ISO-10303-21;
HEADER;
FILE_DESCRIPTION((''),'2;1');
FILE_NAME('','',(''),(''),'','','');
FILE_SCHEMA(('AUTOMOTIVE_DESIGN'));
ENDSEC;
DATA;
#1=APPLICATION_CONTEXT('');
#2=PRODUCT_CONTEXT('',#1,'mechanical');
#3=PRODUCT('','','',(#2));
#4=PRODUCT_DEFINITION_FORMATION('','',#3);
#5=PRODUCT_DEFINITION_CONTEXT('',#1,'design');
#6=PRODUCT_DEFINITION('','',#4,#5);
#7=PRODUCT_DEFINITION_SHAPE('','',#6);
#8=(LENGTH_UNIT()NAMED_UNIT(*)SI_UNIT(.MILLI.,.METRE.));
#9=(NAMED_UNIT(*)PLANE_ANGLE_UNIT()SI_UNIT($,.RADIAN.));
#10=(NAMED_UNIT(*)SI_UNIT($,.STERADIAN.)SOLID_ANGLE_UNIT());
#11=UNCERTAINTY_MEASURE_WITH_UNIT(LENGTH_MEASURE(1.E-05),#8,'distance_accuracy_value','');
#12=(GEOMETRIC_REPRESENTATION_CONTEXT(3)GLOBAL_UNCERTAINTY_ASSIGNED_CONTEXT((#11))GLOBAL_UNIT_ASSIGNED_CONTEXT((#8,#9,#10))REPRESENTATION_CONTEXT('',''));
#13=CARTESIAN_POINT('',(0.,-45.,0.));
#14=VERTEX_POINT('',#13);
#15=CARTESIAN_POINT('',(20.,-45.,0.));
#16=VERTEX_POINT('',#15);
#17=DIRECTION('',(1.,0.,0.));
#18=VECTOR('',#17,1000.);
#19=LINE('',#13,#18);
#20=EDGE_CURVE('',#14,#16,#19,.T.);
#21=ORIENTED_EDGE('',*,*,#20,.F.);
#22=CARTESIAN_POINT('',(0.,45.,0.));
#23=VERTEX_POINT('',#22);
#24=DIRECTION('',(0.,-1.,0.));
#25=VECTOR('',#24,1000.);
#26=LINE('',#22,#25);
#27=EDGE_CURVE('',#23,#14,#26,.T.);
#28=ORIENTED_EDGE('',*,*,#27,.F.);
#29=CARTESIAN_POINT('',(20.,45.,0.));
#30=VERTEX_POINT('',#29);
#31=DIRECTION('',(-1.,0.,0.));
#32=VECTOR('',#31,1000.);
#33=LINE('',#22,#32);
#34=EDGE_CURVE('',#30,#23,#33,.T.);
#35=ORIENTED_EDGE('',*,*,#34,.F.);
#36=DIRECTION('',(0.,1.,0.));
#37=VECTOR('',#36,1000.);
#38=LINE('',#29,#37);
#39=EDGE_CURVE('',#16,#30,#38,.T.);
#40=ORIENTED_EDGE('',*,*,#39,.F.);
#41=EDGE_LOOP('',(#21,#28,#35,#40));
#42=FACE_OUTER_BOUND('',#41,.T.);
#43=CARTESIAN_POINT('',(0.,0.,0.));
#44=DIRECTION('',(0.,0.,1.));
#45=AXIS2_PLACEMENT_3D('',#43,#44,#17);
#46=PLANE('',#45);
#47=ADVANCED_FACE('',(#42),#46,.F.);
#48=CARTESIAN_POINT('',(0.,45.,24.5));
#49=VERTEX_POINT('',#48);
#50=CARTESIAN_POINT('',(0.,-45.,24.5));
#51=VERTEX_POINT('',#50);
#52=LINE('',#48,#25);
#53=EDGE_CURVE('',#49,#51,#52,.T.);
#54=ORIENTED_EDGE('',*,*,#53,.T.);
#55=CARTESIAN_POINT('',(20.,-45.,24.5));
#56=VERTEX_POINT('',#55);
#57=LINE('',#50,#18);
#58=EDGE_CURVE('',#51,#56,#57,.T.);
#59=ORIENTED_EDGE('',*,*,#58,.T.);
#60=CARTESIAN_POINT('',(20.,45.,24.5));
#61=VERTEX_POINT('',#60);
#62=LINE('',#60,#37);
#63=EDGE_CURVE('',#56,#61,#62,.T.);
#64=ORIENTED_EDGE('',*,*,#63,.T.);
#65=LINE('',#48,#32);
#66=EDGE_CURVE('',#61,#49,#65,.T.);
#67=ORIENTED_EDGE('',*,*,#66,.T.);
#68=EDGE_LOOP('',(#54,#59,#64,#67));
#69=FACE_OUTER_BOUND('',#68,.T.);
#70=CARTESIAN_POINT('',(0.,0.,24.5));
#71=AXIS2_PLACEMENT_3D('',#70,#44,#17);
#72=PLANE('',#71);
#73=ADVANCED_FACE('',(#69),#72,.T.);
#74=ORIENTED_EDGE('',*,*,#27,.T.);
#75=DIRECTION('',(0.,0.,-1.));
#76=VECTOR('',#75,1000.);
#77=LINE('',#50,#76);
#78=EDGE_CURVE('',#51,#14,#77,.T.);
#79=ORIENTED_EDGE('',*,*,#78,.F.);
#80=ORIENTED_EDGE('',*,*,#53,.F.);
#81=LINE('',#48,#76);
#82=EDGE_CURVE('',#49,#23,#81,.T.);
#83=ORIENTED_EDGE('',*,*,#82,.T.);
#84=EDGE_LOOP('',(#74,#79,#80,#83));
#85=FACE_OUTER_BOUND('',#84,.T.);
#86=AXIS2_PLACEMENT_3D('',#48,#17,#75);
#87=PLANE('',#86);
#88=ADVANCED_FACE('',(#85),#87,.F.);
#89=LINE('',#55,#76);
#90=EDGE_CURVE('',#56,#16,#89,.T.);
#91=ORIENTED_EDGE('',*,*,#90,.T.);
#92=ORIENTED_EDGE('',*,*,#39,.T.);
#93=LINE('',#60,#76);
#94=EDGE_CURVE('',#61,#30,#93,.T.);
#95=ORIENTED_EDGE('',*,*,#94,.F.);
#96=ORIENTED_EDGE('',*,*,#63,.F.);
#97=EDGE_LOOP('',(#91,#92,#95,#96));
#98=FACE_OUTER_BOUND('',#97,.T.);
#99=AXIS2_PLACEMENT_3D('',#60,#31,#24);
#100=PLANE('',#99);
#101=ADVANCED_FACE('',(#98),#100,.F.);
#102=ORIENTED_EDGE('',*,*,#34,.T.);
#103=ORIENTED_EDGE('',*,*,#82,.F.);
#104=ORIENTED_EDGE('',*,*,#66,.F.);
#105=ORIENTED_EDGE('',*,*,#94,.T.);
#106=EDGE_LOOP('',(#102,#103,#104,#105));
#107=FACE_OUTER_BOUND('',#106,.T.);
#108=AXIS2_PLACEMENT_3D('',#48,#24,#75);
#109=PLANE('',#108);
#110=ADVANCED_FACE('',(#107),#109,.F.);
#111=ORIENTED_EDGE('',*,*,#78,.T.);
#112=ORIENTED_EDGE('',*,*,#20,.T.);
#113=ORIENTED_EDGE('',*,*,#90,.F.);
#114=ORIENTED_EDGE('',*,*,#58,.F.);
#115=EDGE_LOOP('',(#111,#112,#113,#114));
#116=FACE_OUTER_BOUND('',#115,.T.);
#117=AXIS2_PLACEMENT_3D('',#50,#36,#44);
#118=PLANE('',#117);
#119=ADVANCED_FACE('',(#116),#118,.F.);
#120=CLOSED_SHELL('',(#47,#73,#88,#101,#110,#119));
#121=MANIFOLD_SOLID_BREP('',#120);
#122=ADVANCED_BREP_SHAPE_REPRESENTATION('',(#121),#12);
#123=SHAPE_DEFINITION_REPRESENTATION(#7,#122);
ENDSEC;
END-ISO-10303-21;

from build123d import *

# Parameters (mm, degrees)
SKETCH_1_W      = 20
SKETCH_1_H      = 90
EXTRUDE_1_DEPTH = 24.5


with BuildPart() as part:
    # 草图1 → 凸台-拉伸1 (new body)
    with BuildSketch(Plane.XY):
        with Locations((10, 0)):
            Rectangle(SKETCH_1_W, SKETCH_1_H)
    extrude(amount=EXTRUDE_1_DEPTH)


solid = part.part
